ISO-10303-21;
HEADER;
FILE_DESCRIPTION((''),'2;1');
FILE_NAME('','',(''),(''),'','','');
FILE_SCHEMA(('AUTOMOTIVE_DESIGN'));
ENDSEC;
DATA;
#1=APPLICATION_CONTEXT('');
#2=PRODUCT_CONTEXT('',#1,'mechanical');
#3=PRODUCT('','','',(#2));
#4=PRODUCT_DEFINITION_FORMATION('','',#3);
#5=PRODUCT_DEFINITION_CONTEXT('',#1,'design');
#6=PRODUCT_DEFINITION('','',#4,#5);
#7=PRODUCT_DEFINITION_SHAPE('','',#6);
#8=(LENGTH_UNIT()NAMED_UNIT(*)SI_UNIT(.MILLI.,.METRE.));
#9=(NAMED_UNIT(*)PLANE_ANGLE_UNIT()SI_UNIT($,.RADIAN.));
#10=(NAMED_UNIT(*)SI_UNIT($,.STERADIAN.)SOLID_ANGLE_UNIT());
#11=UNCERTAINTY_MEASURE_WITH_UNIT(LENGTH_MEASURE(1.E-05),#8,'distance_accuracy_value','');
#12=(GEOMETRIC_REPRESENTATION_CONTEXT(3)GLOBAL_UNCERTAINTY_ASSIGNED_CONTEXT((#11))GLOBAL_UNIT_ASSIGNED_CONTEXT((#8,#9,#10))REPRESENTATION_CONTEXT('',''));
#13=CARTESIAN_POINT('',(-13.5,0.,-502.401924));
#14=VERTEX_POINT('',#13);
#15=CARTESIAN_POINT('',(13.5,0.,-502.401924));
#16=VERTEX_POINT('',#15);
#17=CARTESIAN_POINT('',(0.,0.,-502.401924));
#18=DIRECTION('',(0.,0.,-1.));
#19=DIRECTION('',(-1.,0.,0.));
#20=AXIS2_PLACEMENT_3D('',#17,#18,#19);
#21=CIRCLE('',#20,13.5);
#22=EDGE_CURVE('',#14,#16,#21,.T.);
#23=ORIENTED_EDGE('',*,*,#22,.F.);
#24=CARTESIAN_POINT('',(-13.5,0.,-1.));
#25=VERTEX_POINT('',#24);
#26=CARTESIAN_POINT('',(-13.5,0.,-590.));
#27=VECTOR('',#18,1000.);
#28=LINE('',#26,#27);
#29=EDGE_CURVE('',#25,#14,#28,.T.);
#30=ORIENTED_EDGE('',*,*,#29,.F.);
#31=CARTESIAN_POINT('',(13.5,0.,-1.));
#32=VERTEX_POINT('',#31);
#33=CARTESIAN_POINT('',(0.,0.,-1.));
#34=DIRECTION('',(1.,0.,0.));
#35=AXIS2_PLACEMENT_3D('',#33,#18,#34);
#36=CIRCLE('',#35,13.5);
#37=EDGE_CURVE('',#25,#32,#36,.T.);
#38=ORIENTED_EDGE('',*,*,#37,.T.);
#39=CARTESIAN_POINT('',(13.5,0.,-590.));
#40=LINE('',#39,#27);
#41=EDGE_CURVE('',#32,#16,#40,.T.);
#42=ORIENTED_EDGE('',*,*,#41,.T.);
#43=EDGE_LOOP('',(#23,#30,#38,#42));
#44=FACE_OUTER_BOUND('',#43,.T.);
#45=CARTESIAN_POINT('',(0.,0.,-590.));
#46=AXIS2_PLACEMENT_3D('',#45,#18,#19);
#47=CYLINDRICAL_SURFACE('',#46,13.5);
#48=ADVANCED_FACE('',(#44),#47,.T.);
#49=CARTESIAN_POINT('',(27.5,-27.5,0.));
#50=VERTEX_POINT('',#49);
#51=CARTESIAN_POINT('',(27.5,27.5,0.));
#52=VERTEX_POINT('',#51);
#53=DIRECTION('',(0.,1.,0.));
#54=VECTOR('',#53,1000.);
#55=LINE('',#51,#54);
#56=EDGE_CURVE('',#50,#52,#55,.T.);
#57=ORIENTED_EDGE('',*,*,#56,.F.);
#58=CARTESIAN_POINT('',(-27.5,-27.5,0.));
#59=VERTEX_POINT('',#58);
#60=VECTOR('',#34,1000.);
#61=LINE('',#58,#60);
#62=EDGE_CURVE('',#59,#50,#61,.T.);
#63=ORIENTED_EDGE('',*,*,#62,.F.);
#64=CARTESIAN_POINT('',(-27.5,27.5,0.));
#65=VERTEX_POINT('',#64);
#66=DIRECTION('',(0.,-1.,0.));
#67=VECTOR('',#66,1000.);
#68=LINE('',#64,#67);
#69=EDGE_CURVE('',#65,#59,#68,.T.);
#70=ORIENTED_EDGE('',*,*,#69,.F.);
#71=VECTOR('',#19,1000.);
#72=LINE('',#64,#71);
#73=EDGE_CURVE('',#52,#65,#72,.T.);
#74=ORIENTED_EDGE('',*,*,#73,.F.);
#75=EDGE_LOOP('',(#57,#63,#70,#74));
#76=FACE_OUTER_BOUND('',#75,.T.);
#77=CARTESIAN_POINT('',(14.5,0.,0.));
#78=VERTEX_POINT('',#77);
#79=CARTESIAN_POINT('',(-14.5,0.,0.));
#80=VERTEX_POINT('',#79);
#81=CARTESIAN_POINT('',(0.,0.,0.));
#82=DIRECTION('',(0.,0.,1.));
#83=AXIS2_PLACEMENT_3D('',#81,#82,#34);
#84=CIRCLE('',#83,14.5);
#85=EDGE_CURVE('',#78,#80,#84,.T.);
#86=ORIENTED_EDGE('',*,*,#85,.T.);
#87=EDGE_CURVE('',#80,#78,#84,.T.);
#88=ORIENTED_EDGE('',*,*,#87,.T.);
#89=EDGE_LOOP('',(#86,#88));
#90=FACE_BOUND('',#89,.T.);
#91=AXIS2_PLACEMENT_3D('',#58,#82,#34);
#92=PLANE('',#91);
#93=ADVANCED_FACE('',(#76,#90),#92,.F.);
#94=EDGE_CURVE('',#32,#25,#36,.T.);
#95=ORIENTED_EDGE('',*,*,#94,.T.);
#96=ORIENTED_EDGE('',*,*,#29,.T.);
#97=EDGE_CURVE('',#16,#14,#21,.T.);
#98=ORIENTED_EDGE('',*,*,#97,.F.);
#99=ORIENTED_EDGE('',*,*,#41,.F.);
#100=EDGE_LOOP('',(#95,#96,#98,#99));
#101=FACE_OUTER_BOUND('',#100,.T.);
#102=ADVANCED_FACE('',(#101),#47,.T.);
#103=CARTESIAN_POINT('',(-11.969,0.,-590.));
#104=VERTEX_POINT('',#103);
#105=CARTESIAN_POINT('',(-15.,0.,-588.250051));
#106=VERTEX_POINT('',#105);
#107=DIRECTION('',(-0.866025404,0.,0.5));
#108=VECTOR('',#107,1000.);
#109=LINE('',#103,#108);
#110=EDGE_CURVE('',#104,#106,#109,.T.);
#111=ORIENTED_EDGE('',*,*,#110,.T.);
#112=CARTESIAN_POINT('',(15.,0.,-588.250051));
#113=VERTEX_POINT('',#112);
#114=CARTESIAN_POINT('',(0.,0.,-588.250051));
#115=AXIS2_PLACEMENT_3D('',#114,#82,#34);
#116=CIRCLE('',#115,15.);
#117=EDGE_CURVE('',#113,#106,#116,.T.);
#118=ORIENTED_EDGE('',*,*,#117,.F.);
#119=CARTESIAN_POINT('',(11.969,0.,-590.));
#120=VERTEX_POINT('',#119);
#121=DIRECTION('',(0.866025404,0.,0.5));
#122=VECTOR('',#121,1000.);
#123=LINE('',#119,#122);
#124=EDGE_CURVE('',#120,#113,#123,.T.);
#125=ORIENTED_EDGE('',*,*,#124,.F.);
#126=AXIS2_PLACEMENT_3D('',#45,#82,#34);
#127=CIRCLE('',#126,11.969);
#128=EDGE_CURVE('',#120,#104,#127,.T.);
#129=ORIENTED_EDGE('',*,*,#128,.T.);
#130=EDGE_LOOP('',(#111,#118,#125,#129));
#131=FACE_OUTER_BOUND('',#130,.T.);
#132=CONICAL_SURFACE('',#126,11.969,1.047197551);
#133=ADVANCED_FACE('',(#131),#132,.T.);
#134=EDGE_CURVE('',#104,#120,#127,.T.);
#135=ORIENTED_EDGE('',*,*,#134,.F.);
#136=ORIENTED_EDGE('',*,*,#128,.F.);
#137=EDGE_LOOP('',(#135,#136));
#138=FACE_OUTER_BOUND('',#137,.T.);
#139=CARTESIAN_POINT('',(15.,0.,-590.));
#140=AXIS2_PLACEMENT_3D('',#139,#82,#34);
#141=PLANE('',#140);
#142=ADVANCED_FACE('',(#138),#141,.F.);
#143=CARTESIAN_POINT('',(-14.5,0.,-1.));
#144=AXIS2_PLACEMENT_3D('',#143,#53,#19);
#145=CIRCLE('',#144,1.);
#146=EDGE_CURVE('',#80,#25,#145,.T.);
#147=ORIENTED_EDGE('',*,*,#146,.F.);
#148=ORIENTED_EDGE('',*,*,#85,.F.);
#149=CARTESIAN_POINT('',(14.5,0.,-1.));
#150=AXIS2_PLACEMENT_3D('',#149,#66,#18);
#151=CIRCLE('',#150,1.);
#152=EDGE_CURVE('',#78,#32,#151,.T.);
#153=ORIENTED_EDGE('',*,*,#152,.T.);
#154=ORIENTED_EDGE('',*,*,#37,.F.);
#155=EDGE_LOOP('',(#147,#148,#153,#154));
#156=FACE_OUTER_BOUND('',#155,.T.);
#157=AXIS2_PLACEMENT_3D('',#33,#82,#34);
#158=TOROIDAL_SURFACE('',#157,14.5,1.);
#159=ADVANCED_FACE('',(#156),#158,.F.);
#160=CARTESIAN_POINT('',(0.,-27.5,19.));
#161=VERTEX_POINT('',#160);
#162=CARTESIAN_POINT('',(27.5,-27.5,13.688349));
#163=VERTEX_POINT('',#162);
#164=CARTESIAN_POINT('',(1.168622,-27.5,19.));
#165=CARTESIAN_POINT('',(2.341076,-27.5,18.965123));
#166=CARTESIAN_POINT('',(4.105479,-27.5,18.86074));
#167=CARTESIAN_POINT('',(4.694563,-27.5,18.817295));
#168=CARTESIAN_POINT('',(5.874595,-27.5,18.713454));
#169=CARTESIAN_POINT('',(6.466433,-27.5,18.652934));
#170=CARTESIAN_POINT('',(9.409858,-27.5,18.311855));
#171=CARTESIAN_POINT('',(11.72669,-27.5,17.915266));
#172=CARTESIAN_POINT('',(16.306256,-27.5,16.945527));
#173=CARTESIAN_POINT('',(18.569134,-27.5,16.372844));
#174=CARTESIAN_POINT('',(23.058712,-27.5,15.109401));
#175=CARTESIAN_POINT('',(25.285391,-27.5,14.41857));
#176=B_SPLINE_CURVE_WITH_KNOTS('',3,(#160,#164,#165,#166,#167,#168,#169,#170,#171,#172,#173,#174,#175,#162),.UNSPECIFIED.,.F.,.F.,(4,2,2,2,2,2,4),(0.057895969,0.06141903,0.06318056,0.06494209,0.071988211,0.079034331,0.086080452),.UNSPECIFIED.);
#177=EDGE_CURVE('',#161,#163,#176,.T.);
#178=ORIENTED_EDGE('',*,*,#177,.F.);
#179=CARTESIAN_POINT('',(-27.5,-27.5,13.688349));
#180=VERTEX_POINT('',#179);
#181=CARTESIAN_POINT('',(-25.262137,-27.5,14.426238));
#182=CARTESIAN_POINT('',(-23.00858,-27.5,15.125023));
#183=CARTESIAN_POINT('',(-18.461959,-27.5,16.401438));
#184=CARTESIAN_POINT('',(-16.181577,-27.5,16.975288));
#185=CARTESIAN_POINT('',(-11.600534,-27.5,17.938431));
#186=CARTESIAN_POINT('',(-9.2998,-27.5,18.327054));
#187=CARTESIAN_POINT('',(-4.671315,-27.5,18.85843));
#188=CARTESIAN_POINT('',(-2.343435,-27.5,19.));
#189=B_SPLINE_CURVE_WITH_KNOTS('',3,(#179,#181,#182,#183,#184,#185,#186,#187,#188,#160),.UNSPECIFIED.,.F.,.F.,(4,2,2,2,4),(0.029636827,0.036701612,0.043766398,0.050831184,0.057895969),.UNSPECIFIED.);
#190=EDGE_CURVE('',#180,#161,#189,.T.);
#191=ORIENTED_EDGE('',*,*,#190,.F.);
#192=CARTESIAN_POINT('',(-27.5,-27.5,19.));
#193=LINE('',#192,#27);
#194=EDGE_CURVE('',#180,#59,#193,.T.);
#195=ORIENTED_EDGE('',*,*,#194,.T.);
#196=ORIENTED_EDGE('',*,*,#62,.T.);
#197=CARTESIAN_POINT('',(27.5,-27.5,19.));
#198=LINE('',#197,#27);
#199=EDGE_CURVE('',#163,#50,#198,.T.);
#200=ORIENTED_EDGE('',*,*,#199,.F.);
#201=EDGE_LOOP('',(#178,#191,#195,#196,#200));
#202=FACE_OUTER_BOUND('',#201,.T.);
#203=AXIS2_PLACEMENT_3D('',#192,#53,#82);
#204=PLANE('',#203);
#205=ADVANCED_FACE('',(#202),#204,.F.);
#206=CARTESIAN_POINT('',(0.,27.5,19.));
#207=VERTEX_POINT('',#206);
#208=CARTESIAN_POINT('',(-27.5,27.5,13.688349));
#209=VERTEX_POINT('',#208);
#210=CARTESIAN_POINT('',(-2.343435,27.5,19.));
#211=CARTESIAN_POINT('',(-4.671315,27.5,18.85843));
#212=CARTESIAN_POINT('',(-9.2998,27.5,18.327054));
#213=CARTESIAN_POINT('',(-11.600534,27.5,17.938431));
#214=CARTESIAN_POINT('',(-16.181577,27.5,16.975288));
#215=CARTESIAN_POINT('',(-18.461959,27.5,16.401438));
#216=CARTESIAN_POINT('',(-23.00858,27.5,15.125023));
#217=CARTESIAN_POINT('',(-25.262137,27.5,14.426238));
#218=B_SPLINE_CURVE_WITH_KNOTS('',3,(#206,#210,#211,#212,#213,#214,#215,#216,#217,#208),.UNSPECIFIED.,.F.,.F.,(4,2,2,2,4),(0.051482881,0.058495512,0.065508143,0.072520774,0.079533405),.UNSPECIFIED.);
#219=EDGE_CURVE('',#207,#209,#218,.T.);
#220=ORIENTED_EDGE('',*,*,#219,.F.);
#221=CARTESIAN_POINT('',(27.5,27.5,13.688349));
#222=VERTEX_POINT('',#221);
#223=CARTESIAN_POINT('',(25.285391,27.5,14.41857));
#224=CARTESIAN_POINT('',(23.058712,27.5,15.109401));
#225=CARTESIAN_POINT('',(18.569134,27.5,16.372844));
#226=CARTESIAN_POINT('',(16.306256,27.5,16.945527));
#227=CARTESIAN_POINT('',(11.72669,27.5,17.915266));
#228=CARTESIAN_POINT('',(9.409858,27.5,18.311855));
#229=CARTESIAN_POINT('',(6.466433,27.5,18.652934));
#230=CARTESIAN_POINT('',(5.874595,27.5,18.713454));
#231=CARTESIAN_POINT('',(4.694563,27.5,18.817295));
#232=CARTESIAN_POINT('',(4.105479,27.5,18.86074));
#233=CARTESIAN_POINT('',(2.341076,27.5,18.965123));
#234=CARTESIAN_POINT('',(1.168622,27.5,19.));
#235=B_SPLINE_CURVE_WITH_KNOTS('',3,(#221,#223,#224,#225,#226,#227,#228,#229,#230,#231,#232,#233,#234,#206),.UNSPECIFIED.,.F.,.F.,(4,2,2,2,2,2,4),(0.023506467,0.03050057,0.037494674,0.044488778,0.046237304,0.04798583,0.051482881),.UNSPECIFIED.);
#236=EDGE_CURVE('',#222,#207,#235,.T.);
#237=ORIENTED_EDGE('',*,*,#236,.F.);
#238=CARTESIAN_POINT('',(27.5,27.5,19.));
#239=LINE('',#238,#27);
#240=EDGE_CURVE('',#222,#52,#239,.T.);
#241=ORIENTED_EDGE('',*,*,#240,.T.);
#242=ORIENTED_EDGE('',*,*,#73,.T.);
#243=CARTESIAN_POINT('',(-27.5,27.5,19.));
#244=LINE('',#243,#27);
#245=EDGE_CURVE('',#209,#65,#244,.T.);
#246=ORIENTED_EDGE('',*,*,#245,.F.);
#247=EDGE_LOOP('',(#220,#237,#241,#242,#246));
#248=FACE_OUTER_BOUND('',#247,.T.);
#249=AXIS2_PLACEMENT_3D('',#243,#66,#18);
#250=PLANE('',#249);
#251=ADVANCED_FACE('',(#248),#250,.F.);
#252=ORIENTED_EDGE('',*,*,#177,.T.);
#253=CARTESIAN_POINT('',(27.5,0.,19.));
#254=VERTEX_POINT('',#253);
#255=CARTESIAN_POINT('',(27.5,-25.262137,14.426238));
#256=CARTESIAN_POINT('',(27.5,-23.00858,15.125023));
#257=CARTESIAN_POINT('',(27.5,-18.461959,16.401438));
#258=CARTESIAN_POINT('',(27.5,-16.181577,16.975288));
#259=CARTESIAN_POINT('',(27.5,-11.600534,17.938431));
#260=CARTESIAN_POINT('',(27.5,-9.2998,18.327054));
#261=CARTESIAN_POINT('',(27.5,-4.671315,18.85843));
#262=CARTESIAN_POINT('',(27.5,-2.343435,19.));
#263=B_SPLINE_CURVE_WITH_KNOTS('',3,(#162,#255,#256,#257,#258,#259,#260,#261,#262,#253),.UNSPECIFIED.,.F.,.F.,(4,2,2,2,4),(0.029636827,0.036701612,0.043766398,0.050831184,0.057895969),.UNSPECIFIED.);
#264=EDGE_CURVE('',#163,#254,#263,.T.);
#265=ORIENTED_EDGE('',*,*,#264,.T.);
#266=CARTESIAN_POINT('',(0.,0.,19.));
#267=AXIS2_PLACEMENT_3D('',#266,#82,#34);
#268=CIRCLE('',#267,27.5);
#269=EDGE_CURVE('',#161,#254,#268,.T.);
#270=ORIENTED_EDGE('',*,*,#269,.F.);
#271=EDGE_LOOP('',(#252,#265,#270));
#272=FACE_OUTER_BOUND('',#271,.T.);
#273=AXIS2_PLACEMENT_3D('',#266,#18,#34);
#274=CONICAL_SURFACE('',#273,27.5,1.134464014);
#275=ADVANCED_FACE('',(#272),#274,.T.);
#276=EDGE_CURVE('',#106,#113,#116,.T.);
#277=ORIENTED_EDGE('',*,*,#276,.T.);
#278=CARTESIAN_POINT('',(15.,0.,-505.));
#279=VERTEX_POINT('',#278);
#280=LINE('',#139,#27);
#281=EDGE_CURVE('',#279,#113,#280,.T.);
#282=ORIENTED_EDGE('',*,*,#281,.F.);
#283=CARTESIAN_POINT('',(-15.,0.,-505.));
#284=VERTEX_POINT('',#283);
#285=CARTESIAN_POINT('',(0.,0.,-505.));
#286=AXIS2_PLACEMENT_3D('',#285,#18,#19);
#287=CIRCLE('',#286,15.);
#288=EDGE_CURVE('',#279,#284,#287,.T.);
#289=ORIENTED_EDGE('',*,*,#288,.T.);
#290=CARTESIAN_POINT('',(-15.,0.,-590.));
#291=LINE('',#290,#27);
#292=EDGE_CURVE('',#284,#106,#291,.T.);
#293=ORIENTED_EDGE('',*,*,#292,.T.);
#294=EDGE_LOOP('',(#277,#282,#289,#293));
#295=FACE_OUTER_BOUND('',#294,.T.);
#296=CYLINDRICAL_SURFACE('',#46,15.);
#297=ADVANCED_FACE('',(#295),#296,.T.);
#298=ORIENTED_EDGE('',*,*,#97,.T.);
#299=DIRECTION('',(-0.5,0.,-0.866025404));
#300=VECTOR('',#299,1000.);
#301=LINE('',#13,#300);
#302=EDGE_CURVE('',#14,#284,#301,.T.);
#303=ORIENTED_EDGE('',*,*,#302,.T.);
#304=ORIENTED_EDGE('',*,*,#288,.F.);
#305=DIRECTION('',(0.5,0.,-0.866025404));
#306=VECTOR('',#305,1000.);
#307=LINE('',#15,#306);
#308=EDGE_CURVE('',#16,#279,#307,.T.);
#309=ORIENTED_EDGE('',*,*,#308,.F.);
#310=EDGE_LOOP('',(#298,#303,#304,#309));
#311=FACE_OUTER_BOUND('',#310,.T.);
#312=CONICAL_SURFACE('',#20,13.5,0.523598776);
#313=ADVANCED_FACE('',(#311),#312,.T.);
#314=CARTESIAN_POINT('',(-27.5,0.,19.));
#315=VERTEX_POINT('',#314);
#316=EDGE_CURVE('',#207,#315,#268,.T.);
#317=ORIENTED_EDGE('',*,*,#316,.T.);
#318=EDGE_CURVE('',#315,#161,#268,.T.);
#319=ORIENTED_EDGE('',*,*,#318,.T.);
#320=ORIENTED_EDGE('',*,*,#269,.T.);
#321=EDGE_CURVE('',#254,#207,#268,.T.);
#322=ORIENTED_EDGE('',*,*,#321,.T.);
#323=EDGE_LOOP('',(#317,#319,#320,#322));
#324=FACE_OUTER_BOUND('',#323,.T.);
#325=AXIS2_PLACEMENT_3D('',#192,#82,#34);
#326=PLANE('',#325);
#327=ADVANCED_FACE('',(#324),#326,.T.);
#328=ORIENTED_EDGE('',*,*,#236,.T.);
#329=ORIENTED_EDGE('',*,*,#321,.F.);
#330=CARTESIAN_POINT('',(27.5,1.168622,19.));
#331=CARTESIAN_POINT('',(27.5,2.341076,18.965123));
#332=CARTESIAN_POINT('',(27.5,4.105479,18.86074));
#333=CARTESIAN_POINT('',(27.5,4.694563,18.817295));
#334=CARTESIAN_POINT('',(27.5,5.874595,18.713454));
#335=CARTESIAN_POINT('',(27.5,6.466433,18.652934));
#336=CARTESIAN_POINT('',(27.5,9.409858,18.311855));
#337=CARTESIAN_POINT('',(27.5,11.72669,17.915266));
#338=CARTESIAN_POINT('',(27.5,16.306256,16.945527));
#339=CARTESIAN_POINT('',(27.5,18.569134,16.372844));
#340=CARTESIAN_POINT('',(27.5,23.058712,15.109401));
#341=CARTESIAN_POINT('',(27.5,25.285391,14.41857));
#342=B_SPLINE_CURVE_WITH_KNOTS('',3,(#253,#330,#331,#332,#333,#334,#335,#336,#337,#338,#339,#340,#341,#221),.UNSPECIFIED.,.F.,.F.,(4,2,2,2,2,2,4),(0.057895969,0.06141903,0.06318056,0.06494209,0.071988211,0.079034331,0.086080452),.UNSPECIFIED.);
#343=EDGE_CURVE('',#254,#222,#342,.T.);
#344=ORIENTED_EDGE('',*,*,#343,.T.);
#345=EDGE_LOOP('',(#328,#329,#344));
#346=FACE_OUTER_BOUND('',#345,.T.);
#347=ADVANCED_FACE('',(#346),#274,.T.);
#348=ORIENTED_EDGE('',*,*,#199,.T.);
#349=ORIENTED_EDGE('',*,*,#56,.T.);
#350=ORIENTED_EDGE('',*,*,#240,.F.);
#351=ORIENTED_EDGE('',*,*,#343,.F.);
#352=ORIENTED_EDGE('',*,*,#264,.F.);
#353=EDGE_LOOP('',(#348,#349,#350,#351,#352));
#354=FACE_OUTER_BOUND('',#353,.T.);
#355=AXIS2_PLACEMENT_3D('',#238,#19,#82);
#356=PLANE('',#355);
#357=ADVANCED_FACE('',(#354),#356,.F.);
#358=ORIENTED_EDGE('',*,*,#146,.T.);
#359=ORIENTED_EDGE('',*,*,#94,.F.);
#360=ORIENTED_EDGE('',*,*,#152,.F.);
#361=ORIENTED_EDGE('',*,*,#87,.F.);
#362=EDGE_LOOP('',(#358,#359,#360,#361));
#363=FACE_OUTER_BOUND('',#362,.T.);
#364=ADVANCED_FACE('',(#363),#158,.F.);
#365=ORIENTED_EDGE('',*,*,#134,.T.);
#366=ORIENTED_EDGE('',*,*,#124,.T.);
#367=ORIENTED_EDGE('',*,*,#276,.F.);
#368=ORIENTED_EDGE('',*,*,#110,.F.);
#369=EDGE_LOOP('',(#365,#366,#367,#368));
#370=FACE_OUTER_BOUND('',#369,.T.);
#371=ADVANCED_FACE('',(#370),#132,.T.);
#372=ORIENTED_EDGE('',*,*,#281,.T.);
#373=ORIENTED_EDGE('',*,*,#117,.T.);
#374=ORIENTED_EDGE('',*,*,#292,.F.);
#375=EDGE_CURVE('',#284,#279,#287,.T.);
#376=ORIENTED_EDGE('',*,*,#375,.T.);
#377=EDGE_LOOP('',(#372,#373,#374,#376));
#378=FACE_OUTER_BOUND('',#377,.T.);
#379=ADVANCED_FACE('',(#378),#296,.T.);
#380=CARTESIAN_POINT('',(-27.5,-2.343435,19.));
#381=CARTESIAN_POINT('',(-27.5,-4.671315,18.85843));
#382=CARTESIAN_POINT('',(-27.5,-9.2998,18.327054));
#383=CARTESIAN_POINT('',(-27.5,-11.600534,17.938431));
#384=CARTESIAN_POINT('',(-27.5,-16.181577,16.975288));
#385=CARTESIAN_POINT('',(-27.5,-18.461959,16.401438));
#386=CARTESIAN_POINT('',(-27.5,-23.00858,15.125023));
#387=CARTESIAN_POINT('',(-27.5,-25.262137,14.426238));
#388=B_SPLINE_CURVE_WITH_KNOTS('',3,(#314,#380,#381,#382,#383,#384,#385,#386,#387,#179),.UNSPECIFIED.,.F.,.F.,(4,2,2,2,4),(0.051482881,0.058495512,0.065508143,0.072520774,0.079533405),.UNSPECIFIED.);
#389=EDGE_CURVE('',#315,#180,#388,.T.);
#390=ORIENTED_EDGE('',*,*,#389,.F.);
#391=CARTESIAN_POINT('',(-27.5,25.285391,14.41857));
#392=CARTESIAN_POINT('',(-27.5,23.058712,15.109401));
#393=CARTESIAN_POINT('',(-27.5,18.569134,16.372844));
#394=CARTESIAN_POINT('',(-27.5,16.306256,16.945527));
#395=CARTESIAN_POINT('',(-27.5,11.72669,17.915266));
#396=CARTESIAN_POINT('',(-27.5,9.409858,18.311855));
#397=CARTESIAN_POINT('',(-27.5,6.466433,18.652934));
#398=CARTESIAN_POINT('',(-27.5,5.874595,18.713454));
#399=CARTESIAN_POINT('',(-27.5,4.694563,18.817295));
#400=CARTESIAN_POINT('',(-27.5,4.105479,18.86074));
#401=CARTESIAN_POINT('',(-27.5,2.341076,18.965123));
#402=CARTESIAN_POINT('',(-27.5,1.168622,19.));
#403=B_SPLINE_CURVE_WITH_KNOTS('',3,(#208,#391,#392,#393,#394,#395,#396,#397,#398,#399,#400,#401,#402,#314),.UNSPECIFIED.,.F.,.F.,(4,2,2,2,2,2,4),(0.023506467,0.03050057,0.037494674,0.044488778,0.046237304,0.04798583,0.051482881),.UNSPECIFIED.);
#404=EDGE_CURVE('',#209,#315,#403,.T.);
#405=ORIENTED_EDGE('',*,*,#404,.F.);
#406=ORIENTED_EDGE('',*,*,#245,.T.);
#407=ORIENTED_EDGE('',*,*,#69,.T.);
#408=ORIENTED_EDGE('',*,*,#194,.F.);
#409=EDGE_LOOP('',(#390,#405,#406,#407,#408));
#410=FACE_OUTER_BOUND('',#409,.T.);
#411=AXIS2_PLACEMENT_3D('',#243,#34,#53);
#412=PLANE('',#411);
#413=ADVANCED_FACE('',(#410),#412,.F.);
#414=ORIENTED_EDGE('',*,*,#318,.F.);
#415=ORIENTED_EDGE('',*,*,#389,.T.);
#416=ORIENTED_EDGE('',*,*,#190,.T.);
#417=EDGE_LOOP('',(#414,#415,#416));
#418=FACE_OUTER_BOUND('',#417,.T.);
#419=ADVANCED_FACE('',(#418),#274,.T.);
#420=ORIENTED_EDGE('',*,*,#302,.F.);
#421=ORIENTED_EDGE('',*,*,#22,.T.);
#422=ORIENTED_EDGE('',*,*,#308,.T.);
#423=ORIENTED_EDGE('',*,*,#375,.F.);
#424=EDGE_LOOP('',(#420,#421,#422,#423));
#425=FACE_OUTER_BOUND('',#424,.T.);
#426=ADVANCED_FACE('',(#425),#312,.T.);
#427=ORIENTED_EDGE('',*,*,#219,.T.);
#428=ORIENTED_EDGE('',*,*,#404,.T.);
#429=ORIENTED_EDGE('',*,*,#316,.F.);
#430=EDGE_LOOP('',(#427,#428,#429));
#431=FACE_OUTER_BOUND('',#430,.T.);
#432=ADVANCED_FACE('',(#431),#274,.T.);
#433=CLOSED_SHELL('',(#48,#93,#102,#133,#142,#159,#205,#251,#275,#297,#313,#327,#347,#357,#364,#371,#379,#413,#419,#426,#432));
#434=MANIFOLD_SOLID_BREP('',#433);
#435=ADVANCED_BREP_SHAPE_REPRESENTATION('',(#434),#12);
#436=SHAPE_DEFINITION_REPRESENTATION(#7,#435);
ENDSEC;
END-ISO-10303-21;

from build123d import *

# Parameters (mm, degrees)
SKETCH1_W          = 55
SKETCH1_H          = 55
BASE_EXTRUDE_DEPTH = 19
SKETCH4_OUTSIDE_W  = 262.948
SKETCH4_OUTSIDE_H  = 262.948
SKETCH4_OUTSIDE_R  = 27.5
CUT_EXTRUDE1_DEPTH = 44.283946216
CUT_EXTRUDE1_DRAFT = -65
FILLET1_R          = 1


with BuildPart() as part:
    # Sketch1 → Base-Extrude (new body)
    with BuildSketch(Plane.XY):
        Rectangle(SKETCH1_W, SKETCH1_H)
    extrude(amount=BASE_EXTRUDE_DEPTH)


with BuildPart() as cut_extrude1_tool:
    # Sketch4 outside → Cut-Extrude1 (with draft: the straight prism first)
    with BuildSketch(Plane.XY.offset(19)):
        Rectangle(SKETCH4_OUTSIDE_W, SKETCH4_OUTSIDE_H)
        Circle(SKETCH4_OUTSIDE_R, mode=Mode.SUBTRACT)
    extrude(amount=-CUT_EXTRUDE1_DEPTH)
    # Cut-Extrude1: the draft: its side faces are tilted about the plane it starts from
    cut_extrude1_sides = [cut_extrude1_tool.faces().sort_by_distance(p)[0] for p in [
        (0, -131.474, -3.141973108),
        (131.474, 0, -3.141973108),
        (0, 131.474, -3.141973108),
        (-131.474, 0, -3.141973108),
        (-27.5, 0, -3.141973108),
    ]]
    draft(cut_extrude1_sides, Plane.XY.offset(19), CUT_EXTRUDE1_DRAFT)


with BuildPart() as part_1:
    add(part.part)

    # Cut-Extrude1: cut by cut_extrude1_tool
    add(cut_extrude1_tool.part, mode=Mode.SUBTRACT)

    # Sketch2 → Boss-Revolve1 (revolve)
    with BuildSketch(Plane(origin=(0, 0, 0), x_dir=(1, 0, 0), z_dir=(0, 1, 0)), mode=Mode.PRIVATE) as boss_revolve1_sk:
        Polygon((0, 0), (13.5, 0), (13.5, 502.401923789), (15, 505), (15, 590), (0, 590), align=None)
    revolve(boss_revolve1_sk.sketch.rotate(Axis((0, 0, -590), (0, 0, 1)), 180), axis=Axis((0, 0, -590), (0, 0, 1)))

    # Fillet1
    fillet1_edges = [part_1.edges().sort_by_distance(p)[0] for p in [
        (13.5, 0, 0),
    ]]
    fillet(fillet1_edges, radius=FILLET1_R)

    # Sketch3 → Cut-Revolve1 (revolve, cut)
    with BuildSketch(Plane(origin=(0, 0, 0), x_dir=(1, 0, 0), z_dir=(0, 1, 0))):
        Polygon((11.969, 590), (15, 591.749948666), (15, 588.250051334), align=None)
    revolve(axis=Axis((0, 0, 0), (0, 0, -1)), mode=Mode.SUBTRACT)


solid = part_1.part
